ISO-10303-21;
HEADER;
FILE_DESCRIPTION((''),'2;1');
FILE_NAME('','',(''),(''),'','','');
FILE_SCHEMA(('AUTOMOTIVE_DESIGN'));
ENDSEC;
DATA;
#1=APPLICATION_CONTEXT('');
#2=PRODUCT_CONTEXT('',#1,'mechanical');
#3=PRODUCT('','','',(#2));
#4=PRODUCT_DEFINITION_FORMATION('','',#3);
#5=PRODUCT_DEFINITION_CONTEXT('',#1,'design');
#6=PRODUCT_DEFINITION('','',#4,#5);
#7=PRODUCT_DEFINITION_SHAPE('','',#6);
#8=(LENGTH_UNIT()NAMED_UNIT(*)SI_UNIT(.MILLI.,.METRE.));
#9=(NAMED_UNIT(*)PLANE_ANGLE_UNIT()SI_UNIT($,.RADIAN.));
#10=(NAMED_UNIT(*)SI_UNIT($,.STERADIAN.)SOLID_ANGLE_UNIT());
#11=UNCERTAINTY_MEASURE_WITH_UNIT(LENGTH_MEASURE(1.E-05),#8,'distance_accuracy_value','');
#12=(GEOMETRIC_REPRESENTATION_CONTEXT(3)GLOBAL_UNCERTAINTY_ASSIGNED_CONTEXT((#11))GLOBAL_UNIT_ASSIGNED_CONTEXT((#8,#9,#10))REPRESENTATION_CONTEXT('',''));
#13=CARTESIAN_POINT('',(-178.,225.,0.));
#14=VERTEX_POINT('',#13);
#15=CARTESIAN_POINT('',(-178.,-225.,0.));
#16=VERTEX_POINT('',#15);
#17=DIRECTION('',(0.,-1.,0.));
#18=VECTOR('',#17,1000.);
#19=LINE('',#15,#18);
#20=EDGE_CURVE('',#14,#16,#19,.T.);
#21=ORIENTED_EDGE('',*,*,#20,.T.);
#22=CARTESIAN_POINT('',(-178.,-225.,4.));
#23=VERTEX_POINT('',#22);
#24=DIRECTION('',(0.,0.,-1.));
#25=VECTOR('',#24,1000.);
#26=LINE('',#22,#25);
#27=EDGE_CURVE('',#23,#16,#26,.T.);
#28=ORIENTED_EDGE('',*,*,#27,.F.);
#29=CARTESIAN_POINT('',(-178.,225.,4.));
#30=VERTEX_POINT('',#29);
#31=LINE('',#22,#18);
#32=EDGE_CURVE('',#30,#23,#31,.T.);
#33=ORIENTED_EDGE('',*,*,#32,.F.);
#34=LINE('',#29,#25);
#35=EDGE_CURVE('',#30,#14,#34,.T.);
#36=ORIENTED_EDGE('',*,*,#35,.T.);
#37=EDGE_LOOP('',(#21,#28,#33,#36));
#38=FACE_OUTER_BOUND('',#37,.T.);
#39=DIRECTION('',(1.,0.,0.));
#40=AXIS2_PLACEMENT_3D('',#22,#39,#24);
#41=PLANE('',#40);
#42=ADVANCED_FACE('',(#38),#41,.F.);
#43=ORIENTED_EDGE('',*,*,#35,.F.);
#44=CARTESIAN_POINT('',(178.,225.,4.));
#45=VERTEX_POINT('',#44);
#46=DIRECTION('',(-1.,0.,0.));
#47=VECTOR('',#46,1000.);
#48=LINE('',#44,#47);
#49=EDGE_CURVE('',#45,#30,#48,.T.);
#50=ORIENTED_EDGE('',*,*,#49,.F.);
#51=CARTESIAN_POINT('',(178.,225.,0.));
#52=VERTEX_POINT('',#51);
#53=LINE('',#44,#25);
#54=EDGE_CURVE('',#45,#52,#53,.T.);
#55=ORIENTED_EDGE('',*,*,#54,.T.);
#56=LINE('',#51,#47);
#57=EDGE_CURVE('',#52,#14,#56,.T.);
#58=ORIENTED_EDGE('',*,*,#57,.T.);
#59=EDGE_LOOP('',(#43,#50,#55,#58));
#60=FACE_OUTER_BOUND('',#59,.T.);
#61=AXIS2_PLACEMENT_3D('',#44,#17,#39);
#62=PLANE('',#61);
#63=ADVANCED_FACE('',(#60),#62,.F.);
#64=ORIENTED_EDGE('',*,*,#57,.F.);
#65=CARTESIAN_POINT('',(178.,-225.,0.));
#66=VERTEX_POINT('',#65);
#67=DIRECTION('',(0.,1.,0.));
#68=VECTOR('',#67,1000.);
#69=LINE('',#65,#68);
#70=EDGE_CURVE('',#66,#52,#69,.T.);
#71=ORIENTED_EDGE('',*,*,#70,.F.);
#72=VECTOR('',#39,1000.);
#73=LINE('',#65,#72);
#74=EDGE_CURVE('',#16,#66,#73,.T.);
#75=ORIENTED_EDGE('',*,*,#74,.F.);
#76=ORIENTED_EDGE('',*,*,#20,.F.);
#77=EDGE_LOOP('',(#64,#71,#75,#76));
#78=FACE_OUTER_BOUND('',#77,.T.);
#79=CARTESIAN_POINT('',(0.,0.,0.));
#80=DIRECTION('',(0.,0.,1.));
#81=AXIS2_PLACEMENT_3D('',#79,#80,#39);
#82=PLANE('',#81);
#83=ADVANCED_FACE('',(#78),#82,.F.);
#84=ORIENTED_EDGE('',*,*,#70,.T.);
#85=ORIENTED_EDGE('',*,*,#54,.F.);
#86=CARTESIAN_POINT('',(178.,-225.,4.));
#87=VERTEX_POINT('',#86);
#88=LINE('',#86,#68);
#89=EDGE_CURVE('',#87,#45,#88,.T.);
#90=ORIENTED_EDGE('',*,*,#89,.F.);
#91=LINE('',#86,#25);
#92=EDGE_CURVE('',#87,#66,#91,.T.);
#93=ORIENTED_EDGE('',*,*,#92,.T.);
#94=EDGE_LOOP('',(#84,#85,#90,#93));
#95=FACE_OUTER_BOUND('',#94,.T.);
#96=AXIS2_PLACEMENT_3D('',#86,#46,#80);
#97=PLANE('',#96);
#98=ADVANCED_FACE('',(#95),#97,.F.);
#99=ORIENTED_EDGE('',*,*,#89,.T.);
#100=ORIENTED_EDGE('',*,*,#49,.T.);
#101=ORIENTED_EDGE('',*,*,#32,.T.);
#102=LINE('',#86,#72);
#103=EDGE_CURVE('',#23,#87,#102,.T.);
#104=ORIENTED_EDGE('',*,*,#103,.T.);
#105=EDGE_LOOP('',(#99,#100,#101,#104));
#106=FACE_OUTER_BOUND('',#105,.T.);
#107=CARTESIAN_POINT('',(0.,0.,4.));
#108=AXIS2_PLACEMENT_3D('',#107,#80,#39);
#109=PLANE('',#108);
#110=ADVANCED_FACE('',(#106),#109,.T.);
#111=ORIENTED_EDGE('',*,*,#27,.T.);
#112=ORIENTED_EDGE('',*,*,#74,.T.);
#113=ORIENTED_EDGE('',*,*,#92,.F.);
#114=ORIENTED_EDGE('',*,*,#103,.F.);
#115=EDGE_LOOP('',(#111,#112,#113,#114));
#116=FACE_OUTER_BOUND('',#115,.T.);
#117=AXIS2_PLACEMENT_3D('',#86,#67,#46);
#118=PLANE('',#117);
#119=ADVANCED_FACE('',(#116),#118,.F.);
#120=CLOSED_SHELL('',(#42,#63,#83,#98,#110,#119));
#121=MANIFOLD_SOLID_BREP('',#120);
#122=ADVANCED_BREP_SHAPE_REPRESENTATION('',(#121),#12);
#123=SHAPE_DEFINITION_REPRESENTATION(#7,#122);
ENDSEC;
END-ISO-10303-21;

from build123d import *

# Parameters (mm, degrees)
SKETCH_1_W      = 356
SKETCH_1_H      = 450
EXTRUDE_1_DEPTH = 4


with BuildPart() as part:
    # 草图1 → 凸台-拉伸1 (new body)
    with BuildSketch(Plane.XY):
        Rectangle(SKETCH_1_W, SKETCH_1_H)
    extrude(amount=EXTRUDE_1_DEPTH)


solid = part.part
